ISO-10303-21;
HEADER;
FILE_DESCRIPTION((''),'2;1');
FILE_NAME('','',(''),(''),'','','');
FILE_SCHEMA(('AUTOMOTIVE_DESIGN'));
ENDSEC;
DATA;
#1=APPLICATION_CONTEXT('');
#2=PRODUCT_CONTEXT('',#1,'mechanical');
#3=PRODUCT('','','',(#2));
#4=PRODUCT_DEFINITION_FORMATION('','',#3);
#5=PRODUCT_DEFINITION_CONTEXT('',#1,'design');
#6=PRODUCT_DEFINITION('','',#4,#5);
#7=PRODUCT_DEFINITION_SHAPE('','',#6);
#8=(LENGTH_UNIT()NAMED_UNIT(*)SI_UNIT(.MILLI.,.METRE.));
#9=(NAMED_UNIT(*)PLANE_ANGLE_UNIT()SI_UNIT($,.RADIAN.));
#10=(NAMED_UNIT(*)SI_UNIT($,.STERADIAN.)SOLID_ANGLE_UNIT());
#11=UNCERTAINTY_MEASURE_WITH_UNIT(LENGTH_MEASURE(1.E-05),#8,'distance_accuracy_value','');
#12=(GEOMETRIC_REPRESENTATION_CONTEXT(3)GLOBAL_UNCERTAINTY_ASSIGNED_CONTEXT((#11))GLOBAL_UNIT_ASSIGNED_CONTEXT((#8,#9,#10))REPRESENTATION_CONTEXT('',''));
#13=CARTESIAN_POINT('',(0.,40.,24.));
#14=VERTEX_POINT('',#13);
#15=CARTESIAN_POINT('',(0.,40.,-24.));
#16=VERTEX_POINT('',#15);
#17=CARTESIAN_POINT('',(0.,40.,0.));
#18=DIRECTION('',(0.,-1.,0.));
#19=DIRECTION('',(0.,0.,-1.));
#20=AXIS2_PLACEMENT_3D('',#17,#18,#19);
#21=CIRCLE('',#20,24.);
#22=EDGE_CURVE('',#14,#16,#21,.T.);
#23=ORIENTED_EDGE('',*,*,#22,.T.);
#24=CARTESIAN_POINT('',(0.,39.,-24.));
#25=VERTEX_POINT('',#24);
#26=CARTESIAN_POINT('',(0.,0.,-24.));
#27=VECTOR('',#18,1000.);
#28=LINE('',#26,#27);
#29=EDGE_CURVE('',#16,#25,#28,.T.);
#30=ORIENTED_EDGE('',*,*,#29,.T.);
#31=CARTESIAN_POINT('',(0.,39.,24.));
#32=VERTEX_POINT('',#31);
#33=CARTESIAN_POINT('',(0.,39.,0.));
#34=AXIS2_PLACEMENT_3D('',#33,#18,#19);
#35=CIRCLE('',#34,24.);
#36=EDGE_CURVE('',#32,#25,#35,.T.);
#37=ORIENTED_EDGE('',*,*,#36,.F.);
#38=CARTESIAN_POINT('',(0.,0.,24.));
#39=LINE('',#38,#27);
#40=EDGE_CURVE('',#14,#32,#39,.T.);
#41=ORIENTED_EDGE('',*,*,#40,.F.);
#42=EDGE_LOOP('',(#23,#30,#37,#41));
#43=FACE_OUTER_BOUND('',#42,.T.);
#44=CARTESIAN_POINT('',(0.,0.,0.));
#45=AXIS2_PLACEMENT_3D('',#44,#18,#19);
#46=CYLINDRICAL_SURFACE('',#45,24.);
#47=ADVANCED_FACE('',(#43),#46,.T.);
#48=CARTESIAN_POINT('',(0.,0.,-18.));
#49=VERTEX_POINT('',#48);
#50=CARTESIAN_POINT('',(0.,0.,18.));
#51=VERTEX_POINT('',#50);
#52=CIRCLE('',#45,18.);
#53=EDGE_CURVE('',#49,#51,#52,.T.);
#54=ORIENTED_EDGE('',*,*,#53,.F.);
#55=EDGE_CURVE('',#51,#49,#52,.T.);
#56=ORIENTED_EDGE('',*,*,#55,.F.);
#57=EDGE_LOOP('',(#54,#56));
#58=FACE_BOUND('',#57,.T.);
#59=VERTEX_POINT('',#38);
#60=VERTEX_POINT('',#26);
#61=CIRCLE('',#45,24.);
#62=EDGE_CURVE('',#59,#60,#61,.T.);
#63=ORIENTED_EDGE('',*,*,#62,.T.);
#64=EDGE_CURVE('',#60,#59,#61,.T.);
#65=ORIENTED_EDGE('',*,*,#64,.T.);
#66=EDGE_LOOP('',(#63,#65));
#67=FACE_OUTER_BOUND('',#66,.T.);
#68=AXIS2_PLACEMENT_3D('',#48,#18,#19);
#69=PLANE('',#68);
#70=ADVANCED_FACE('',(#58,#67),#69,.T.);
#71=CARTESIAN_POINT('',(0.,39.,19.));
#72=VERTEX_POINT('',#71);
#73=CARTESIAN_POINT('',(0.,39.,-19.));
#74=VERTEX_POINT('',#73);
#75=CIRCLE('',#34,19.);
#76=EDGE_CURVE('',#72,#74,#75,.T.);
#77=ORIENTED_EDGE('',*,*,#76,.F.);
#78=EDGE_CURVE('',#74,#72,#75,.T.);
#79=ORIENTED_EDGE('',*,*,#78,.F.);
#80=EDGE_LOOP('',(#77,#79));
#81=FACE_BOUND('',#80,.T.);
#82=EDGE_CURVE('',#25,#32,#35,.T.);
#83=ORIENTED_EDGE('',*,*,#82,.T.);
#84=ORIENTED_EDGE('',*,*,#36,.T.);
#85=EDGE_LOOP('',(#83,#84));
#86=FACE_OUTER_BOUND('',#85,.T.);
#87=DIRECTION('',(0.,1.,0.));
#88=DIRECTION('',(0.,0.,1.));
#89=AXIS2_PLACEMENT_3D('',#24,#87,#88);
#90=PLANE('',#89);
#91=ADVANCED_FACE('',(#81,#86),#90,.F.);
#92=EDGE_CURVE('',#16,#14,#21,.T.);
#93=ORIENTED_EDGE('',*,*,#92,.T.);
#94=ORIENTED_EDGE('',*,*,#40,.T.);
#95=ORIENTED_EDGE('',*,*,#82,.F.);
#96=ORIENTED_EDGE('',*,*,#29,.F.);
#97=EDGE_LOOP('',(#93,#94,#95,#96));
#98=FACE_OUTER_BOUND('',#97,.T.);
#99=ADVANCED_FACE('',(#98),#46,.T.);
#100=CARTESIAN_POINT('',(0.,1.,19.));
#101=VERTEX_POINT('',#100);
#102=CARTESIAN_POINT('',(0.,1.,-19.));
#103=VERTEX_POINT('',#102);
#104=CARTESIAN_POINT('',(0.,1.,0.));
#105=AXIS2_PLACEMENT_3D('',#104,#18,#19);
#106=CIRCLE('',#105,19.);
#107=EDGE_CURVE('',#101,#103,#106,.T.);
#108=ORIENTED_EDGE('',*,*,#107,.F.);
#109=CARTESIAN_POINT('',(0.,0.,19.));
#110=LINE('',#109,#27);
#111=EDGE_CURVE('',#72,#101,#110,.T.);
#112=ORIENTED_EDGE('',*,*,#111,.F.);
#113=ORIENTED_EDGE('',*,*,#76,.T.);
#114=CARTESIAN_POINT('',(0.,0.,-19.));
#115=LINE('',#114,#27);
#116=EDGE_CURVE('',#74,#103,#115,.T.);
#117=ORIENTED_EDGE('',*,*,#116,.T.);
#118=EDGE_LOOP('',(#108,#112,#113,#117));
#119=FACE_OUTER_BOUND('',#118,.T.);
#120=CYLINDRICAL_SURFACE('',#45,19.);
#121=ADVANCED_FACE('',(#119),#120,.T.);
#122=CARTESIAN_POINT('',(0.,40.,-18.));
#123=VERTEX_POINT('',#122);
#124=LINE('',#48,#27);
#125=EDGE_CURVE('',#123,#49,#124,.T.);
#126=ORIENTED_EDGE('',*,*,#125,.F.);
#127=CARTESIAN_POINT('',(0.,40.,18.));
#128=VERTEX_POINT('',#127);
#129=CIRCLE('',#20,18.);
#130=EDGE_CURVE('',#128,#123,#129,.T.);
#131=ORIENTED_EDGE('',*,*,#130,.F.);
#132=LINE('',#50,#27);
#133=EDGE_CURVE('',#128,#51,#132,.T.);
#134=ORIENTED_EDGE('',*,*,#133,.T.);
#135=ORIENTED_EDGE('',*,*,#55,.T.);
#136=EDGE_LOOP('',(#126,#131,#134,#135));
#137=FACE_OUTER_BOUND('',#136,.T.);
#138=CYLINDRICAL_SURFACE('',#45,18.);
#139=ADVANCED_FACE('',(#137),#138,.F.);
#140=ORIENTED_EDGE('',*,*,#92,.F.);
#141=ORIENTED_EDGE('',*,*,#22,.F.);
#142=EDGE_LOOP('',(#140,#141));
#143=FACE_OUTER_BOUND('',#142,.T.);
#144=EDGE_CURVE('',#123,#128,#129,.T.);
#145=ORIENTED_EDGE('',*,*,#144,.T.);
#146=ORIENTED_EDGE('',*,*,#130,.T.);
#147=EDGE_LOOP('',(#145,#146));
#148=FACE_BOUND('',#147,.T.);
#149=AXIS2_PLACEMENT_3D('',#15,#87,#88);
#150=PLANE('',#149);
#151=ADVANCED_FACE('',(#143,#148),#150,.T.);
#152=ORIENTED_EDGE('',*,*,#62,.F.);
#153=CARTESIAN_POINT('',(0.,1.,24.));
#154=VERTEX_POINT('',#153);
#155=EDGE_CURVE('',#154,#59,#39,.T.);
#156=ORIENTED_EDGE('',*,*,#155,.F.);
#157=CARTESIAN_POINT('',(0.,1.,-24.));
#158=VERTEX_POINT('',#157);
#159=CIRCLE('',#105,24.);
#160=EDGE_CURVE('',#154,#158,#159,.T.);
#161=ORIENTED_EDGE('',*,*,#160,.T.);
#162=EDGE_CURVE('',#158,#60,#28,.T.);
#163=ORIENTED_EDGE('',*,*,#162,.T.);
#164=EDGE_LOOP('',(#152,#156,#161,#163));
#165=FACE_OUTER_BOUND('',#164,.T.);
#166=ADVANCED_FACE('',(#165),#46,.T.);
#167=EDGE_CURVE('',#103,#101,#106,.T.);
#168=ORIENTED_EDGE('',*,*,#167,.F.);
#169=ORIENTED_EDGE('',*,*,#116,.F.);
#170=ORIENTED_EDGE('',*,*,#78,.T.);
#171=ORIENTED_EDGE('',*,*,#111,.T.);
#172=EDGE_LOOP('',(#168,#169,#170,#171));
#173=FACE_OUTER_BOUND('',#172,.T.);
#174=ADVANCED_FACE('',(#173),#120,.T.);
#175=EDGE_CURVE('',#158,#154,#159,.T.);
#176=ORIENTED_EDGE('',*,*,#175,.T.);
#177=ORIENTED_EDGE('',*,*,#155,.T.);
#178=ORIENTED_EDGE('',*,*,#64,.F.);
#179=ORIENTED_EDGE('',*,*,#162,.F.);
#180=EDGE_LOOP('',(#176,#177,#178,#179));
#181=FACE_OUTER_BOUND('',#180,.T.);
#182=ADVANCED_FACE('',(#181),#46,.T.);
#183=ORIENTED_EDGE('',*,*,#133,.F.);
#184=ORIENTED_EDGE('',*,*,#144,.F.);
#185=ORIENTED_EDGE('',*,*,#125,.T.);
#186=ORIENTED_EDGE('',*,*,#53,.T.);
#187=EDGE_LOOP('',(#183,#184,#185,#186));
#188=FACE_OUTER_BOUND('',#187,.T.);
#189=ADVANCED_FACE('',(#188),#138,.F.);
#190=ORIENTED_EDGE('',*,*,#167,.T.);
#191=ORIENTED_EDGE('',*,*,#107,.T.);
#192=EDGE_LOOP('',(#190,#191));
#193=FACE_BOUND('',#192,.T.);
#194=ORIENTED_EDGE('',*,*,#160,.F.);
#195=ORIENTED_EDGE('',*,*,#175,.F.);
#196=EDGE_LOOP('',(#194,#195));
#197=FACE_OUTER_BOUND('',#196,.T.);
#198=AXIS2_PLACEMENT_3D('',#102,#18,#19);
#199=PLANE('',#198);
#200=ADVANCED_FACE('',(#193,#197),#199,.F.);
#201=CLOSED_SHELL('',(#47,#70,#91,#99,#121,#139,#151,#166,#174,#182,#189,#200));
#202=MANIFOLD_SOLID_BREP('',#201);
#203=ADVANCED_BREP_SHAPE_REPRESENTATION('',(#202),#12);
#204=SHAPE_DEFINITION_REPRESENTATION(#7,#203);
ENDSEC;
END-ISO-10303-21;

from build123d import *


with BuildPart() as part:
    # Sketch2 → Revolve2 (revolve)
    with BuildSketch(Plane(origin=(0, 0, 0), x_dir=(0, 0, -1), z_dir=(1, 0, 0))):
        Polygon((24, 40), (24, 39), (19, 39), (19, 1), (24, 1), (24, 0), (18, 0), (18, 40), align=None)
    revolve(axis=Axis((0, 0, 0), (0, 1, 0)))


solid = part.part
